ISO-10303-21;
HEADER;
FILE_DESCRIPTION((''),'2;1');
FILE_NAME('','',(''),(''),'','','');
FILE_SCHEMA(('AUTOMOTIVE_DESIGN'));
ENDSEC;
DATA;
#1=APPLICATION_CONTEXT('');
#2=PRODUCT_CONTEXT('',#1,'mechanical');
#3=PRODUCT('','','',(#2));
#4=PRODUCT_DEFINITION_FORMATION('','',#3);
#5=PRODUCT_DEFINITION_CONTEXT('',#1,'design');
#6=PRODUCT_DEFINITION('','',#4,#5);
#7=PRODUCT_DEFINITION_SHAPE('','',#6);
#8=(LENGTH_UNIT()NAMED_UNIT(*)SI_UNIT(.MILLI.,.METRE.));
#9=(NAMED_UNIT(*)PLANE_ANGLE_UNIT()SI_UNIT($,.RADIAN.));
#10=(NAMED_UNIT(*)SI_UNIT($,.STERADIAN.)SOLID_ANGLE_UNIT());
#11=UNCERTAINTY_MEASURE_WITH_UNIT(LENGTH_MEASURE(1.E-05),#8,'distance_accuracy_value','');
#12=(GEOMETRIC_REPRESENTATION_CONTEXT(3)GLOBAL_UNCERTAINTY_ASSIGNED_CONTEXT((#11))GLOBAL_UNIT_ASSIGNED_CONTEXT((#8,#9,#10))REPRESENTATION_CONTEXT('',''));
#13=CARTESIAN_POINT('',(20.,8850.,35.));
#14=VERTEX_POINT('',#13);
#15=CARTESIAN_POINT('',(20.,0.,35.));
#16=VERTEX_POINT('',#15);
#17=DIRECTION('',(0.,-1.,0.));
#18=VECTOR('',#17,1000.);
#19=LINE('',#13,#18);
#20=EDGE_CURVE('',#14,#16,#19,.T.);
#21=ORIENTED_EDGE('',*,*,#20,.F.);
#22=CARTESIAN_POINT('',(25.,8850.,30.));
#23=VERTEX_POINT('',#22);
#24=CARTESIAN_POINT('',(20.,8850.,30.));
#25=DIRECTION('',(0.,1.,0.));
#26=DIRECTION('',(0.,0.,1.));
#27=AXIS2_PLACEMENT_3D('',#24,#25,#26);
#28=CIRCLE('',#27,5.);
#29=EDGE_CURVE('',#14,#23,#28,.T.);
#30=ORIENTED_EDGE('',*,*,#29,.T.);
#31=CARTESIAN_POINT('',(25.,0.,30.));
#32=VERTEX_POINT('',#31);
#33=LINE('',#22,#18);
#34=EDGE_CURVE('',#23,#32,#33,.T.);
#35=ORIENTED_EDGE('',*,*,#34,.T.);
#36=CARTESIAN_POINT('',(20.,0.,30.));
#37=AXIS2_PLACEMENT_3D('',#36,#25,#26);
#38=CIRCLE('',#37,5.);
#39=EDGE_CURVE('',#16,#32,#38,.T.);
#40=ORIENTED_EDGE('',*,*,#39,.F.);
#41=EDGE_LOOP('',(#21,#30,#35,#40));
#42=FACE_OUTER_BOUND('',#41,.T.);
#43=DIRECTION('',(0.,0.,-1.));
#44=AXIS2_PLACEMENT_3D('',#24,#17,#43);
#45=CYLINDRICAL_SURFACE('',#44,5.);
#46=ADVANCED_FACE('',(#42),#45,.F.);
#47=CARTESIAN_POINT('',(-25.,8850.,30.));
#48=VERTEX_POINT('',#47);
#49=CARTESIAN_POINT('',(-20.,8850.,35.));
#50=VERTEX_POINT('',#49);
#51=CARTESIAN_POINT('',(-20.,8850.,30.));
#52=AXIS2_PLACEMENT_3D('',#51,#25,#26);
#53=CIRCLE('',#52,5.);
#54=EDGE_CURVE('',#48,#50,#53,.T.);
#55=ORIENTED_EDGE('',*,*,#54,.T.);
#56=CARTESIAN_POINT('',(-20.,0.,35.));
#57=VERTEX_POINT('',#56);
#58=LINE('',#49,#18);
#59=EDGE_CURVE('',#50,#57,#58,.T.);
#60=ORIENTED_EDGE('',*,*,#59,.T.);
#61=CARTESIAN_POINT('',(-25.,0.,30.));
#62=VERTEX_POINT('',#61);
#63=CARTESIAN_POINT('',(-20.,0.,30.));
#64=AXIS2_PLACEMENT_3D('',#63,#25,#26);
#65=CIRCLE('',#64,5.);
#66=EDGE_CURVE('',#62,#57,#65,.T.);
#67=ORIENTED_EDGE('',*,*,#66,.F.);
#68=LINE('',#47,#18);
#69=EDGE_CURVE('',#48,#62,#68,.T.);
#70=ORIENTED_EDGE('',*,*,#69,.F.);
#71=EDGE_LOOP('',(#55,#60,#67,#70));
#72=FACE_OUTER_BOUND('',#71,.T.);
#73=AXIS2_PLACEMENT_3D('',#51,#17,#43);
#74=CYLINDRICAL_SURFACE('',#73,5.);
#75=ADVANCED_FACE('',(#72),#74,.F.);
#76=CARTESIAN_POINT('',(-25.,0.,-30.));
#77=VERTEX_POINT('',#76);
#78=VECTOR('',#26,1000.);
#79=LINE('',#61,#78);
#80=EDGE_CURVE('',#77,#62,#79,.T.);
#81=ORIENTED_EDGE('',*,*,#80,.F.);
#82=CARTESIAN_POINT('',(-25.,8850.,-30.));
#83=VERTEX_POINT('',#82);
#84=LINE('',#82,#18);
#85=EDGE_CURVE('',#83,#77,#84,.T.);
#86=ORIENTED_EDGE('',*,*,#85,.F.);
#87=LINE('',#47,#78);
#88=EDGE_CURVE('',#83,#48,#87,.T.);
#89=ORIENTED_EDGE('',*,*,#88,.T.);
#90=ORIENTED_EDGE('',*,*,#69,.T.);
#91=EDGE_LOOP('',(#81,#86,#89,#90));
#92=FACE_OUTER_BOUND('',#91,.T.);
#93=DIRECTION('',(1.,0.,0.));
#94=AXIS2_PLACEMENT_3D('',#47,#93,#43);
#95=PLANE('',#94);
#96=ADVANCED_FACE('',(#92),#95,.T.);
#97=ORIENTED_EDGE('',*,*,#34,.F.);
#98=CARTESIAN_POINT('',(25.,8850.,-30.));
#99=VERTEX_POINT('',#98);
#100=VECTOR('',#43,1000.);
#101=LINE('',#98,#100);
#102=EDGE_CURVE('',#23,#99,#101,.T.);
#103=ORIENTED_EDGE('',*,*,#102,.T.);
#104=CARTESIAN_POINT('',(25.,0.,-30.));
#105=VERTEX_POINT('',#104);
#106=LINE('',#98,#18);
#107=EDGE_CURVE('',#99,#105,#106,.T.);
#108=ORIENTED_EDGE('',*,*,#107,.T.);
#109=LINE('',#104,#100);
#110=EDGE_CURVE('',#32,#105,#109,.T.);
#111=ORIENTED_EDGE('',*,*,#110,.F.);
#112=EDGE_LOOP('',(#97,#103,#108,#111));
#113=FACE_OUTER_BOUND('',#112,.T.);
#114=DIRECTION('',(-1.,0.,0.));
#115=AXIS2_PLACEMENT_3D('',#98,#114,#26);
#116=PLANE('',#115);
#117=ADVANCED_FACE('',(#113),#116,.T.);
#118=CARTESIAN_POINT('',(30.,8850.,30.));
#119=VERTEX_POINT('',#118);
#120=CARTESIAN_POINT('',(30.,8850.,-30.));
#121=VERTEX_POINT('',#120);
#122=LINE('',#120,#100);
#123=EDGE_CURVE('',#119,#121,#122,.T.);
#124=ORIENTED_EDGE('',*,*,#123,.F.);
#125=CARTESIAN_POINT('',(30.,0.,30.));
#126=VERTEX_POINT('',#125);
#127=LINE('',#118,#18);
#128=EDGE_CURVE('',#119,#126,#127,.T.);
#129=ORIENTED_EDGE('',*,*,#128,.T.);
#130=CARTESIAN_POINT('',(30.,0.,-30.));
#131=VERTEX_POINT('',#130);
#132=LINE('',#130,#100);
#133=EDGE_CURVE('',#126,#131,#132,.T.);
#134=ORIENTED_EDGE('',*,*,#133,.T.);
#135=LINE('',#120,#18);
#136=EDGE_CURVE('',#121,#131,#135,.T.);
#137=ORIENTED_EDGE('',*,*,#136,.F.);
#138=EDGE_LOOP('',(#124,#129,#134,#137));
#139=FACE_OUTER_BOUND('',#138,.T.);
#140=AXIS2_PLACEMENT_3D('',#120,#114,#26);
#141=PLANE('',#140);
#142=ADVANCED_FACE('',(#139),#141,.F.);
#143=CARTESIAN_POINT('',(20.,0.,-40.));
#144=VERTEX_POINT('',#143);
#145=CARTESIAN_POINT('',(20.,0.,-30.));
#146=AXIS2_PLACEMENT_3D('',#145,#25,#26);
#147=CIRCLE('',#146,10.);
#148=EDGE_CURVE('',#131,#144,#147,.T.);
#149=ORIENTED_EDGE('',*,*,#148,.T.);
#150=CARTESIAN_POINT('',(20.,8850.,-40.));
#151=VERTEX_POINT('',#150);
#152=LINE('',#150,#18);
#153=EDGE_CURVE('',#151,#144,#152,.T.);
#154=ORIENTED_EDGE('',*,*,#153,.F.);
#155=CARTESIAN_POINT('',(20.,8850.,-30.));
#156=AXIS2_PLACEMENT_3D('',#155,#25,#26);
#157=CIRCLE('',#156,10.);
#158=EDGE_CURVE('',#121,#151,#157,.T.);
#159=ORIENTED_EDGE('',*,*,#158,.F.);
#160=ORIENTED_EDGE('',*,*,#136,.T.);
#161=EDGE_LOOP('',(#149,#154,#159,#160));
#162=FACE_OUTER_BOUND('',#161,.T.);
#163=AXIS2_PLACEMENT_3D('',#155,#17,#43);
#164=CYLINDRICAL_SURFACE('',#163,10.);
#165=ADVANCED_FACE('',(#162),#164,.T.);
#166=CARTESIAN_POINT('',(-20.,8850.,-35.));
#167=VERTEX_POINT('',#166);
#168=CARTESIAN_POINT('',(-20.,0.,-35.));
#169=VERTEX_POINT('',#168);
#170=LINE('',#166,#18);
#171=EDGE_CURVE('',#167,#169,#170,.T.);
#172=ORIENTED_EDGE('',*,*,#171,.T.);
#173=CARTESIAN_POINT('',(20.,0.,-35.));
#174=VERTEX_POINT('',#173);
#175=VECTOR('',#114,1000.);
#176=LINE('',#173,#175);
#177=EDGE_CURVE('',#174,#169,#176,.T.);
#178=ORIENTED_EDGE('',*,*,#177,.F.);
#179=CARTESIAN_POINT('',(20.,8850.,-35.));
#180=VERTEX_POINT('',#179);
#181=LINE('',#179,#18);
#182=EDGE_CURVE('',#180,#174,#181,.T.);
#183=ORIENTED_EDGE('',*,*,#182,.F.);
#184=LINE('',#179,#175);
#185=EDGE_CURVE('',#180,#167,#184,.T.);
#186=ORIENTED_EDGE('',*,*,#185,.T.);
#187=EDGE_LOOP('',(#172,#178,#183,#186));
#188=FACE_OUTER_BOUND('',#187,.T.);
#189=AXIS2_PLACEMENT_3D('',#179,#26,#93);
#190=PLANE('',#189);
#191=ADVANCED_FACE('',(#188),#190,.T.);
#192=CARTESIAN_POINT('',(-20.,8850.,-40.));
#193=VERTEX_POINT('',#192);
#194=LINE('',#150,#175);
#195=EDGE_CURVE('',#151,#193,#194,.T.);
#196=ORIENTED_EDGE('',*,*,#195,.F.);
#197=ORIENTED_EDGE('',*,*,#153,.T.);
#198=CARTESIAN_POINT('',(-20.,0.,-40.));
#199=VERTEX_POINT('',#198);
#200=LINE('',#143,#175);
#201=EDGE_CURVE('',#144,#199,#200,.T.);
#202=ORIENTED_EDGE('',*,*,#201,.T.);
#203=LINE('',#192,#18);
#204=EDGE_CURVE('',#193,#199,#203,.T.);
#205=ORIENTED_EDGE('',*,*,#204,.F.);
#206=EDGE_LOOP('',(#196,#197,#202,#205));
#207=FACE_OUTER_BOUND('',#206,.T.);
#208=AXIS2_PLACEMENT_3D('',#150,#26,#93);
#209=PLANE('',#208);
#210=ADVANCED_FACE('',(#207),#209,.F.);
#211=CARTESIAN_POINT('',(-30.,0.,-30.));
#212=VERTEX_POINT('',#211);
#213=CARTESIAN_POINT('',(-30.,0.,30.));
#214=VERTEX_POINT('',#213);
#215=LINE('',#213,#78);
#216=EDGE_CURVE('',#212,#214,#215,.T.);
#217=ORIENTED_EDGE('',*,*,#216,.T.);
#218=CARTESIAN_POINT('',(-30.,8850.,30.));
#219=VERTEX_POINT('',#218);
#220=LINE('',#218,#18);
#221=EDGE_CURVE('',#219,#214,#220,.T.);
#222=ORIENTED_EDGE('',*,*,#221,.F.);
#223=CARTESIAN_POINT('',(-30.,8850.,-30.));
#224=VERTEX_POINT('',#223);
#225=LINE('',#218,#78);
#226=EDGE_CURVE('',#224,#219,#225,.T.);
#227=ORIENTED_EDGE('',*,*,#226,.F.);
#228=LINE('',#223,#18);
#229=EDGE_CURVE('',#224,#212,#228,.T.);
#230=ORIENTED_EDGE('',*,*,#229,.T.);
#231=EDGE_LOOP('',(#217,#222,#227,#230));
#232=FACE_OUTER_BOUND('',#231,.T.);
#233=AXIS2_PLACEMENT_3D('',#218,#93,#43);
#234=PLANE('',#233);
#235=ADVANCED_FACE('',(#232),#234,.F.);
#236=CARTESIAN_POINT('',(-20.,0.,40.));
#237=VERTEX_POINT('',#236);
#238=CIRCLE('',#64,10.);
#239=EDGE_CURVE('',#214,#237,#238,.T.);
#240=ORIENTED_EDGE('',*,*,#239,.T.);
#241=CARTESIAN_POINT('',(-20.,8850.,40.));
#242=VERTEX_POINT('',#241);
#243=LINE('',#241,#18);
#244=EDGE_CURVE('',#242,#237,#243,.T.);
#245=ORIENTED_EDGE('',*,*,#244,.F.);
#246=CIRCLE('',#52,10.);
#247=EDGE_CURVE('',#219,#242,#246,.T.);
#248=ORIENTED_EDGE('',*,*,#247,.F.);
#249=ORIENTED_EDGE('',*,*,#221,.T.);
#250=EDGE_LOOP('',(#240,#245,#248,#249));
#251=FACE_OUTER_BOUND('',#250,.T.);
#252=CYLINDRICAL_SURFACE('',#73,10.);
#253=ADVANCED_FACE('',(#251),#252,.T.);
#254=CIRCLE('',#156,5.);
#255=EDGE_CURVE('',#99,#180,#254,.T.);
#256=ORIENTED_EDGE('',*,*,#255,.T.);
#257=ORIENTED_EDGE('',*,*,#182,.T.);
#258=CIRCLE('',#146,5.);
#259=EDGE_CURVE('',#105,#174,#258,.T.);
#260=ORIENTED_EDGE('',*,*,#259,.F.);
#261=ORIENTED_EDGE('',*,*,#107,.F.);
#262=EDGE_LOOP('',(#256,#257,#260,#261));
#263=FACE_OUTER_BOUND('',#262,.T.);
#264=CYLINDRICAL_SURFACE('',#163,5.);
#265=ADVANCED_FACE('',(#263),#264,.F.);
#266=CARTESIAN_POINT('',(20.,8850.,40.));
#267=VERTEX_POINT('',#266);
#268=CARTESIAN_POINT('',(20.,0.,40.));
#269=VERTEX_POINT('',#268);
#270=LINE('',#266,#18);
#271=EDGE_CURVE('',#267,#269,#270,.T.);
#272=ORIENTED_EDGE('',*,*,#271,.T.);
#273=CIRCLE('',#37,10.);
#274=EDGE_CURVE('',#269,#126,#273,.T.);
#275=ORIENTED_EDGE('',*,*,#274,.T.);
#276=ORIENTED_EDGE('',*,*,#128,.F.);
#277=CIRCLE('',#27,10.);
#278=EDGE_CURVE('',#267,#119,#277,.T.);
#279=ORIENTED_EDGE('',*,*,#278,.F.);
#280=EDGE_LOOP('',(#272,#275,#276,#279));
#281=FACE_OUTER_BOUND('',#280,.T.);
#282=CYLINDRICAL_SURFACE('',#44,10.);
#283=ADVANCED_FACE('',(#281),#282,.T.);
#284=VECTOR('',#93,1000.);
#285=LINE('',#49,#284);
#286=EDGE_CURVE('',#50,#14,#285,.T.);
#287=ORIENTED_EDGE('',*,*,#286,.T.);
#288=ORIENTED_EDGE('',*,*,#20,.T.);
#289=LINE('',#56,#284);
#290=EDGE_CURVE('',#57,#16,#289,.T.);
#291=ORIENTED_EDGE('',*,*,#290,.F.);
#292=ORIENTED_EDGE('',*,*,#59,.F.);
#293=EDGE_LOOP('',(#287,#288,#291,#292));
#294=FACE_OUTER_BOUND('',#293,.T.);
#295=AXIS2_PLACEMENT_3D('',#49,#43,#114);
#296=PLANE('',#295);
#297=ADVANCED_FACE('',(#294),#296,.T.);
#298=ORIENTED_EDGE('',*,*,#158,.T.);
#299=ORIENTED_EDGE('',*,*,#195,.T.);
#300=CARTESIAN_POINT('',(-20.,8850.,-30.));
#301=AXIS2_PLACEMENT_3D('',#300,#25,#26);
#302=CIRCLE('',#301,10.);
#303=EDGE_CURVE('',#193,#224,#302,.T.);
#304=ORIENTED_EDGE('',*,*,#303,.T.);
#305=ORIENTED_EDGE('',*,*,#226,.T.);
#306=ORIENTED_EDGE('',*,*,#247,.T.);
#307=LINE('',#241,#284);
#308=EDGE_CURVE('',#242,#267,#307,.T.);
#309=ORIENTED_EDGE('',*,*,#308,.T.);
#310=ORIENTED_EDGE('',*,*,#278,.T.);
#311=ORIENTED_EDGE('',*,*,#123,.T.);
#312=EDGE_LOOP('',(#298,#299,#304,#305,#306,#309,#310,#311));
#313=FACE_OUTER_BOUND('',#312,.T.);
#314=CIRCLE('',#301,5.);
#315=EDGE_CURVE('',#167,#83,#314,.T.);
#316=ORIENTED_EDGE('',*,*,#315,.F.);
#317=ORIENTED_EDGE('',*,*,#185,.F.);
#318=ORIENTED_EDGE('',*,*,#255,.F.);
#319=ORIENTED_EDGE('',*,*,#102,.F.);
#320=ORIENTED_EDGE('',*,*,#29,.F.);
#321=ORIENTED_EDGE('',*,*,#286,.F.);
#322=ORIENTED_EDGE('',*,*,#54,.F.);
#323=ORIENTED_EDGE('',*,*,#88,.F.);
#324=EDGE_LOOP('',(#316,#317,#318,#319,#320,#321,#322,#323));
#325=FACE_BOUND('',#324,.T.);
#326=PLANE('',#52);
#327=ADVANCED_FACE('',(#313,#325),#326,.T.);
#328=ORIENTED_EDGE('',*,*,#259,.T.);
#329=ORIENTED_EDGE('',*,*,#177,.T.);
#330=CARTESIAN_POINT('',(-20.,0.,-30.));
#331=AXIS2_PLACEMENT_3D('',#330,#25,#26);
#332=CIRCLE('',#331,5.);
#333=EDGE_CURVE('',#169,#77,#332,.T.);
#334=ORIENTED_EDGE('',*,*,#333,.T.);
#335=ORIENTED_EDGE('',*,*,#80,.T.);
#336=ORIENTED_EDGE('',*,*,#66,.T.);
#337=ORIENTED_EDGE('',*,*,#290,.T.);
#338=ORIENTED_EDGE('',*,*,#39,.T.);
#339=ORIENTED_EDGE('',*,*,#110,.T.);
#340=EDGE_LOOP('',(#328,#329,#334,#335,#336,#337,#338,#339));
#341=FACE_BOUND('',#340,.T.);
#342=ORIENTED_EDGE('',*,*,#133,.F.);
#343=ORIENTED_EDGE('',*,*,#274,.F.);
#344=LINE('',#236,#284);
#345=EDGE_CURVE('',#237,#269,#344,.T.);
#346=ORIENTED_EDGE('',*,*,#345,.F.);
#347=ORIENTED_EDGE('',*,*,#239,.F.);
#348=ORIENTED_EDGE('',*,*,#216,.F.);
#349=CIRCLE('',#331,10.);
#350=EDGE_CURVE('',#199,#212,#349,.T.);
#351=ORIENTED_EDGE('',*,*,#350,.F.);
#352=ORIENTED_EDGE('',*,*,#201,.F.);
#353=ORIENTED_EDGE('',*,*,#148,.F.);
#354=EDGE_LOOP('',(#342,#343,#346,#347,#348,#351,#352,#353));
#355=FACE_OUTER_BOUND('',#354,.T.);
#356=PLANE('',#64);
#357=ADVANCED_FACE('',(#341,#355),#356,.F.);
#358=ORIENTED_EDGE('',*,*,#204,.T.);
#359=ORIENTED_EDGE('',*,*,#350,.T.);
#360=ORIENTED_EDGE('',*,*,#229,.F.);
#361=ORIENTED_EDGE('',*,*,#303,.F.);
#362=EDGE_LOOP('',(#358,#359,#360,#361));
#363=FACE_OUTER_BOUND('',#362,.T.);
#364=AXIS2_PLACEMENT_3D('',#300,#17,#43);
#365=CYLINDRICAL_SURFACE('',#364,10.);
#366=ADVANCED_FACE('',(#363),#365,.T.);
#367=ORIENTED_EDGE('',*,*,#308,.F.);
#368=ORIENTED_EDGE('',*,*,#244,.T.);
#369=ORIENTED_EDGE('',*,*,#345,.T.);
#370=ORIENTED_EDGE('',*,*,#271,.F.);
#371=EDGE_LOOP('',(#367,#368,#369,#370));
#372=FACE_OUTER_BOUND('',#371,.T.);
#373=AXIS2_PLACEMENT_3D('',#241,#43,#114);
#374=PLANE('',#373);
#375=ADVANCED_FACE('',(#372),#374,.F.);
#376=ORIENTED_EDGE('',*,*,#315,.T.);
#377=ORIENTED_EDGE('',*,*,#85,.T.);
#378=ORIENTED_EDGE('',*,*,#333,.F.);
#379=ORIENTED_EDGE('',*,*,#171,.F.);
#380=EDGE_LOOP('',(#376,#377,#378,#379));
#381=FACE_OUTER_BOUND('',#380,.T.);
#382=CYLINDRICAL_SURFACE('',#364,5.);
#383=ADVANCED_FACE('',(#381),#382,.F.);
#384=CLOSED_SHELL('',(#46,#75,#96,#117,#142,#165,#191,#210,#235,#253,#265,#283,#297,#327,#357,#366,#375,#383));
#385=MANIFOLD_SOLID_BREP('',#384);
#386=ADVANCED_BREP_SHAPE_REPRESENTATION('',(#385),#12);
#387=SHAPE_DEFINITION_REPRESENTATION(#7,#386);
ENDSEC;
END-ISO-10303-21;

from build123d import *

# Parameters (mm, degrees)
COLD_FORMED_HOLLOW_RECTANGULAR_STEEL_GB_DEPTH = 8850


with BuildPart() as part:
    # Sketch1 → Cold-formed hollow rectangular steel (GB/T 6728-2002) 80×60×5(1) (new body)
    with BuildSketch(Plane(origin=(0, 0, 0), x_dir=(-1, 0, 0), z_dir=(0, 1, 0))):
        with BuildLine():
            Line((-20, -40), (20, -40))
            ThreePointArc((20, -40), (27.071067812, -37.071067812), (30, -30))
            Line((30, -30), (30, 30))
            ThreePointArc((30, 30), (27.071067812, 37.071067812), (20, 40))
            Line((20, 40), (-20, 40))
            ThreePointArc((-20, 40), (-27.071067812, 37.071067812), (-30, 30))
            Line((-30, 30), (-30, -30))
            ThreePointArc((-30, -30), (-27.071067812, -37.071067812), (-20, -40))
        make_face()
        with BuildLine():
            Line((-20, -35), (20, -35))
            ThreePointArc((20, -35), (23.535533906, -33.535533906), (25, -30))
            Line((25, -30), (25, 30))
            ThreePointArc((25, 30), (23.535533906, 33.535533906), (20, 35))
            Line((20, 35), (-20, 35))
            ThreePointArc((-20, 35), (-23.535533906, 33.535533906), (-25, 30))
            Line((-25, 30), (-25, -30))
            ThreePointArc((-25, -30), (-23.535533906, -33.535533906), (-20, -35))
        make_face(mode=Mode.SUBTRACT)
    extrude(amount=COLD_FORMED_HOLLOW_RECTANGULAR_STEEL_GB_DEPTH)


solid = part.part
